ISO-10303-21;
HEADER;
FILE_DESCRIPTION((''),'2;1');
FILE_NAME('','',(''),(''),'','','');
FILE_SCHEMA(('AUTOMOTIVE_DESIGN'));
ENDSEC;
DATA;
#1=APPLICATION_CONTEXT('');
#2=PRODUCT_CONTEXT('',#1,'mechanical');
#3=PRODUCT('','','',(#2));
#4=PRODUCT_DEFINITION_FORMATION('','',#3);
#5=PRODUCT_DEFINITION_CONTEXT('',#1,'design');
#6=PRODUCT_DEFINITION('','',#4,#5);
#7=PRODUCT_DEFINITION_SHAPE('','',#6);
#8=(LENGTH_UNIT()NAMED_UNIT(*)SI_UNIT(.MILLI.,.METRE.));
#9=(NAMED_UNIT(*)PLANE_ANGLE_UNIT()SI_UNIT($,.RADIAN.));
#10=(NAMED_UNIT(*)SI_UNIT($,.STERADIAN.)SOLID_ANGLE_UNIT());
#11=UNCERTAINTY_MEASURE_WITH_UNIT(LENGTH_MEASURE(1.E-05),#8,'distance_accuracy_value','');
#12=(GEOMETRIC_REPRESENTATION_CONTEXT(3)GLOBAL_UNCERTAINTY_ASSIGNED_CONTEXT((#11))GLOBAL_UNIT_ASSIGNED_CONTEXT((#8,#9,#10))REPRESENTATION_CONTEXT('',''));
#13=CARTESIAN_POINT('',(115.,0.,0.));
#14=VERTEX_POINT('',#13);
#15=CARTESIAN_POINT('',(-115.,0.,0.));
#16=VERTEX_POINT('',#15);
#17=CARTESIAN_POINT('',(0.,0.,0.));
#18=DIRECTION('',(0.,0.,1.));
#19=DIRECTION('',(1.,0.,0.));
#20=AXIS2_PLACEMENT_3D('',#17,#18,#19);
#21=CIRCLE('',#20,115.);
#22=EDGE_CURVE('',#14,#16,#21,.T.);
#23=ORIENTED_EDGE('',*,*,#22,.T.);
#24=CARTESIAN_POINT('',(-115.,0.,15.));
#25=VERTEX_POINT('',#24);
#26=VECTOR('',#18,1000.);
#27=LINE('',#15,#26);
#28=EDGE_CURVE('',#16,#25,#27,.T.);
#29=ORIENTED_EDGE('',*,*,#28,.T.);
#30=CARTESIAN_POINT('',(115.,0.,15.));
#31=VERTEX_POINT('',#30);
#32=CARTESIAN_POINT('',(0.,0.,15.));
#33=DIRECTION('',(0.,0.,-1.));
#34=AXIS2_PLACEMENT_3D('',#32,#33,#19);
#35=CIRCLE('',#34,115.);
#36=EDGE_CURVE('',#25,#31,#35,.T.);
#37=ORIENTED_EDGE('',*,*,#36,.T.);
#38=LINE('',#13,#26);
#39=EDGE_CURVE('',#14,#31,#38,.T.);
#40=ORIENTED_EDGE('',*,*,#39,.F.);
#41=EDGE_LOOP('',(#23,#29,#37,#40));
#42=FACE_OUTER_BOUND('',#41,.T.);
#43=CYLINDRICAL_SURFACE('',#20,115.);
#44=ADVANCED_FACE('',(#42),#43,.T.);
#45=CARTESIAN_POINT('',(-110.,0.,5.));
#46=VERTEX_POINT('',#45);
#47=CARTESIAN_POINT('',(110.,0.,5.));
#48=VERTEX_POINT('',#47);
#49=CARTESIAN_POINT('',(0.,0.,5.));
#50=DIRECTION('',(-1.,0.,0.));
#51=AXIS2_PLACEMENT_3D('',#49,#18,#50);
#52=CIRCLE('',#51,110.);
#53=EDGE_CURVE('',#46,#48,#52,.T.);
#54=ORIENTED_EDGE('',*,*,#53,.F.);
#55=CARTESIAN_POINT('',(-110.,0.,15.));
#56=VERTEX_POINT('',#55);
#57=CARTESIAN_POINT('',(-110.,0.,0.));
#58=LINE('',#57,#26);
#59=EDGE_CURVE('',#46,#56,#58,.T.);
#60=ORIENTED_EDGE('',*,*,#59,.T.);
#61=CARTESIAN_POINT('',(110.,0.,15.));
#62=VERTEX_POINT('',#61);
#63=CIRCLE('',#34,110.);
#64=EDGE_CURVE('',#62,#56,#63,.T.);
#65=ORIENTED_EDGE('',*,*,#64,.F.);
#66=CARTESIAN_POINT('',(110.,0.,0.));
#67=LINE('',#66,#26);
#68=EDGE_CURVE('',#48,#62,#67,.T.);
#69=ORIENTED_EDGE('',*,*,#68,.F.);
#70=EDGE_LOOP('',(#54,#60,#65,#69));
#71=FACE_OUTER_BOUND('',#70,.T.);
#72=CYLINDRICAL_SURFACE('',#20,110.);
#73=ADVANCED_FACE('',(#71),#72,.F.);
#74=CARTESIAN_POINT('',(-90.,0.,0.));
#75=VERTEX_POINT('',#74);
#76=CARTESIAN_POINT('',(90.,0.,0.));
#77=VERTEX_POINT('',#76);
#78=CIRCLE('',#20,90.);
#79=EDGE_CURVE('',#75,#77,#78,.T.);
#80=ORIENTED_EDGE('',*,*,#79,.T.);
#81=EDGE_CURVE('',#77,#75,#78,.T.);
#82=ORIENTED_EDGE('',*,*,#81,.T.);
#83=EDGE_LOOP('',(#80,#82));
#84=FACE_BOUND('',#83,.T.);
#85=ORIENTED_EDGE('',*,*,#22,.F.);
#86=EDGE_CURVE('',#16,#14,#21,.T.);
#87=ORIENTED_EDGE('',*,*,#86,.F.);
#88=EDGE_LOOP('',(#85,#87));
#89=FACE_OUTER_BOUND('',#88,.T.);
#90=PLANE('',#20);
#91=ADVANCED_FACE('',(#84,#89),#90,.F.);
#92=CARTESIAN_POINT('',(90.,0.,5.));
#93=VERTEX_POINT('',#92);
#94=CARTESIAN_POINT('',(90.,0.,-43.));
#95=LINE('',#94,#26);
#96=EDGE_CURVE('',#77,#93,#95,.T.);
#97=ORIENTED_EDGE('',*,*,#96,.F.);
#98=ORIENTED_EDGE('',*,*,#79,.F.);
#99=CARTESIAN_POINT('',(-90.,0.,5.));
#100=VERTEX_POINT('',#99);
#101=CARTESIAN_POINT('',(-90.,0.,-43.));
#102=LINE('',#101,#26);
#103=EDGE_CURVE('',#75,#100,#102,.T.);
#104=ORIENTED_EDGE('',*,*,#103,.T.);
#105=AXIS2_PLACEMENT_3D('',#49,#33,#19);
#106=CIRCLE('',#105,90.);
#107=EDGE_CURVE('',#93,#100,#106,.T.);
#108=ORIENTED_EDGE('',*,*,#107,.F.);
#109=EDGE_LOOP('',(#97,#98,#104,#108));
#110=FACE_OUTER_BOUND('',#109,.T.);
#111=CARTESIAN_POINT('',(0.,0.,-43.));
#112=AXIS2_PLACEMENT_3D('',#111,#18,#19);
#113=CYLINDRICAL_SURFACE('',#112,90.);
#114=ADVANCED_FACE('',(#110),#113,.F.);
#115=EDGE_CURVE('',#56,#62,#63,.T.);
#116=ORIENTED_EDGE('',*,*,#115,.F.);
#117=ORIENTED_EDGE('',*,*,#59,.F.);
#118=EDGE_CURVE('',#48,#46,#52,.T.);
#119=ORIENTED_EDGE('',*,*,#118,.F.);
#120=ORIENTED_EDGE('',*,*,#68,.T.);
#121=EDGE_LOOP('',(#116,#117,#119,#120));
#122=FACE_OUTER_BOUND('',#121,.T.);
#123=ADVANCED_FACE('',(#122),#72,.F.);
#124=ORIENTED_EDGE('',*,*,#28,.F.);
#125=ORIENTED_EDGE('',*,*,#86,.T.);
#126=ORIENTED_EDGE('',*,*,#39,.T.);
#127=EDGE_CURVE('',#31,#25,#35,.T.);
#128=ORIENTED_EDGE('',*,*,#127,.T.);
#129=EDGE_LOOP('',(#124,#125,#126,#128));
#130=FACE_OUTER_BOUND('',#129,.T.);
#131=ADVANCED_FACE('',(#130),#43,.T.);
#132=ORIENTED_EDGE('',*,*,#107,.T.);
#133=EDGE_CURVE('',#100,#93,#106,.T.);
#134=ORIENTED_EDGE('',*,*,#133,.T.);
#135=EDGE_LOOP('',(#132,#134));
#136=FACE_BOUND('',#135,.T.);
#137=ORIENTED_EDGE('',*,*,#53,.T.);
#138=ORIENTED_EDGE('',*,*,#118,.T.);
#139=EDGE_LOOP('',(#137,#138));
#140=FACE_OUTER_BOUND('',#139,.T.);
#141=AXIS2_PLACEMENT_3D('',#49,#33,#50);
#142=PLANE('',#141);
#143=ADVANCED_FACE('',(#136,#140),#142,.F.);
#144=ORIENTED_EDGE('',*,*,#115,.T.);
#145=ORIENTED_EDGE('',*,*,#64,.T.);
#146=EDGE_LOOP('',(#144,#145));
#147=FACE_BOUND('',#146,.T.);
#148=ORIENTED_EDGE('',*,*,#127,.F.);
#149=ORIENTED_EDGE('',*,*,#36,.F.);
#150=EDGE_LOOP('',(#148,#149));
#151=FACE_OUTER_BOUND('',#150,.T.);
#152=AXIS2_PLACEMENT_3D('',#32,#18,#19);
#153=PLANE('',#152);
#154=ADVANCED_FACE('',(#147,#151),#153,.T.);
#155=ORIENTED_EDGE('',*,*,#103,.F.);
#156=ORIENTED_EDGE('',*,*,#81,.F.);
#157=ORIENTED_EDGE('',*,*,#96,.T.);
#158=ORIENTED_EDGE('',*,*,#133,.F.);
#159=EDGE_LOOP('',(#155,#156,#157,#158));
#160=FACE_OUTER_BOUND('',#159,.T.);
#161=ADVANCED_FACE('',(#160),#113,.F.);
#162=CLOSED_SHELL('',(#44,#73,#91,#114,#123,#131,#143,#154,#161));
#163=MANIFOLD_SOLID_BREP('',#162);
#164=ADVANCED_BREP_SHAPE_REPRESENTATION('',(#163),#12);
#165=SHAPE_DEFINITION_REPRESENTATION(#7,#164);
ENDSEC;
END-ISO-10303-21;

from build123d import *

# Parameters (mm, degrees)
SKETCH_1_R          = 105
EXTRUDE_1_DEPTH     = 30
SKETCH_2_R          = 90
CUT_EXTRUDE_1_DEPTH = 73
SKETCH_3_R          = 100
SKETCH_3_R_2        = 90
CUT_EXTRUDE_2_DEPTH = 25
SKETCH_4_R          = 115
SKETCH_4_R_2        = 110
EXTRUDE_2_DEPTH     = 30
SKETCH_5_R          = 105
SKETCH_5_R_2        = 100
CUT_EXTRUDE_3_DEPTH = 25
SKETCH_6_R          = 110
SKETCH_6_R_2        = 105
EXTRUDE_3_DEPTH     = 5
SKETCH_7_R          = 125
CUT_EXTRUDE_5_DEPTH = 15


with BuildPart() as part:
    # 草图1 → 凸台-拉伸1 (new body)
    with BuildSketch(Plane.XY):
        Circle(SKETCH_1_R)
    extrude(amount=EXTRUDE_1_DEPTH)

    # 草图2 → 切除-拉伸1 (cut)
    with BuildSketch(Plane.XY.offset(30)):
        Circle(SKETCH_2_R)
    extrude(amount=-CUT_EXTRUDE_1_DEPTH, mode=Mode.SUBTRACT)

    # 草图3 → 切除-拉伸2 (cut)
    with BuildSketch(Plane.XY.offset(30)):
        Circle(SKETCH_3_R)
        Circle(SKETCH_3_R_2, mode=Mode.SUBTRACT)
    extrude(amount=-CUT_EXTRUDE_2_DEPTH, mode=Mode.SUBTRACT)

    # 草图5 → 切除-拉伸3 (cut)
    with BuildSketch(Plane.XY.offset(30)):
        Circle(SKETCH_5_R)
        Circle(SKETCH_5_R_2, mode=Mode.SUBTRACT)
    extrude(amount=-CUT_EXTRUDE_3_DEPTH, mode=Mode.SUBTRACT)



with BuildPart() as body_2:
    # 草图4 → 凸台-拉伸2 (new body)
    with BuildSketch(Plane.XY.offset(30)):
        Circle(SKETCH_4_R)
        Circle(SKETCH_4_R_2, mode=Mode.SUBTRACT)
    extrude(amount=-EXTRUDE_2_DEPTH)


with BuildPart() as part_1:
    add(part.part)

    add(body_2.part)  # 凸台-拉伸3 merges body 2
    # 草图6 → 凸台-拉伸3 (add)
    with BuildSketch(Plane(origin=(0, 0, 0), x_dir=(-1, 0, 0), z_dir=(0, 0, -1))):
        with Locations(Location((0, 0, 0), (0, 0, 180))):
            Circle(SKETCH_6_R)
        Circle(SKETCH_6_R_2, mode=Mode.SUBTRACT)
    extrude(amount=-EXTRUDE_3_DEPTH)

    # 草图7 → 切除-拉伸5 (cut)
    with BuildSketch(Plane.XY.offset(30)):
        Circle(SKETCH_7_R)
    extrude(amount=-CUT_EXTRUDE_5_DEPTH, mode=Mode.SUBTRACT)


solid = part_1.part
